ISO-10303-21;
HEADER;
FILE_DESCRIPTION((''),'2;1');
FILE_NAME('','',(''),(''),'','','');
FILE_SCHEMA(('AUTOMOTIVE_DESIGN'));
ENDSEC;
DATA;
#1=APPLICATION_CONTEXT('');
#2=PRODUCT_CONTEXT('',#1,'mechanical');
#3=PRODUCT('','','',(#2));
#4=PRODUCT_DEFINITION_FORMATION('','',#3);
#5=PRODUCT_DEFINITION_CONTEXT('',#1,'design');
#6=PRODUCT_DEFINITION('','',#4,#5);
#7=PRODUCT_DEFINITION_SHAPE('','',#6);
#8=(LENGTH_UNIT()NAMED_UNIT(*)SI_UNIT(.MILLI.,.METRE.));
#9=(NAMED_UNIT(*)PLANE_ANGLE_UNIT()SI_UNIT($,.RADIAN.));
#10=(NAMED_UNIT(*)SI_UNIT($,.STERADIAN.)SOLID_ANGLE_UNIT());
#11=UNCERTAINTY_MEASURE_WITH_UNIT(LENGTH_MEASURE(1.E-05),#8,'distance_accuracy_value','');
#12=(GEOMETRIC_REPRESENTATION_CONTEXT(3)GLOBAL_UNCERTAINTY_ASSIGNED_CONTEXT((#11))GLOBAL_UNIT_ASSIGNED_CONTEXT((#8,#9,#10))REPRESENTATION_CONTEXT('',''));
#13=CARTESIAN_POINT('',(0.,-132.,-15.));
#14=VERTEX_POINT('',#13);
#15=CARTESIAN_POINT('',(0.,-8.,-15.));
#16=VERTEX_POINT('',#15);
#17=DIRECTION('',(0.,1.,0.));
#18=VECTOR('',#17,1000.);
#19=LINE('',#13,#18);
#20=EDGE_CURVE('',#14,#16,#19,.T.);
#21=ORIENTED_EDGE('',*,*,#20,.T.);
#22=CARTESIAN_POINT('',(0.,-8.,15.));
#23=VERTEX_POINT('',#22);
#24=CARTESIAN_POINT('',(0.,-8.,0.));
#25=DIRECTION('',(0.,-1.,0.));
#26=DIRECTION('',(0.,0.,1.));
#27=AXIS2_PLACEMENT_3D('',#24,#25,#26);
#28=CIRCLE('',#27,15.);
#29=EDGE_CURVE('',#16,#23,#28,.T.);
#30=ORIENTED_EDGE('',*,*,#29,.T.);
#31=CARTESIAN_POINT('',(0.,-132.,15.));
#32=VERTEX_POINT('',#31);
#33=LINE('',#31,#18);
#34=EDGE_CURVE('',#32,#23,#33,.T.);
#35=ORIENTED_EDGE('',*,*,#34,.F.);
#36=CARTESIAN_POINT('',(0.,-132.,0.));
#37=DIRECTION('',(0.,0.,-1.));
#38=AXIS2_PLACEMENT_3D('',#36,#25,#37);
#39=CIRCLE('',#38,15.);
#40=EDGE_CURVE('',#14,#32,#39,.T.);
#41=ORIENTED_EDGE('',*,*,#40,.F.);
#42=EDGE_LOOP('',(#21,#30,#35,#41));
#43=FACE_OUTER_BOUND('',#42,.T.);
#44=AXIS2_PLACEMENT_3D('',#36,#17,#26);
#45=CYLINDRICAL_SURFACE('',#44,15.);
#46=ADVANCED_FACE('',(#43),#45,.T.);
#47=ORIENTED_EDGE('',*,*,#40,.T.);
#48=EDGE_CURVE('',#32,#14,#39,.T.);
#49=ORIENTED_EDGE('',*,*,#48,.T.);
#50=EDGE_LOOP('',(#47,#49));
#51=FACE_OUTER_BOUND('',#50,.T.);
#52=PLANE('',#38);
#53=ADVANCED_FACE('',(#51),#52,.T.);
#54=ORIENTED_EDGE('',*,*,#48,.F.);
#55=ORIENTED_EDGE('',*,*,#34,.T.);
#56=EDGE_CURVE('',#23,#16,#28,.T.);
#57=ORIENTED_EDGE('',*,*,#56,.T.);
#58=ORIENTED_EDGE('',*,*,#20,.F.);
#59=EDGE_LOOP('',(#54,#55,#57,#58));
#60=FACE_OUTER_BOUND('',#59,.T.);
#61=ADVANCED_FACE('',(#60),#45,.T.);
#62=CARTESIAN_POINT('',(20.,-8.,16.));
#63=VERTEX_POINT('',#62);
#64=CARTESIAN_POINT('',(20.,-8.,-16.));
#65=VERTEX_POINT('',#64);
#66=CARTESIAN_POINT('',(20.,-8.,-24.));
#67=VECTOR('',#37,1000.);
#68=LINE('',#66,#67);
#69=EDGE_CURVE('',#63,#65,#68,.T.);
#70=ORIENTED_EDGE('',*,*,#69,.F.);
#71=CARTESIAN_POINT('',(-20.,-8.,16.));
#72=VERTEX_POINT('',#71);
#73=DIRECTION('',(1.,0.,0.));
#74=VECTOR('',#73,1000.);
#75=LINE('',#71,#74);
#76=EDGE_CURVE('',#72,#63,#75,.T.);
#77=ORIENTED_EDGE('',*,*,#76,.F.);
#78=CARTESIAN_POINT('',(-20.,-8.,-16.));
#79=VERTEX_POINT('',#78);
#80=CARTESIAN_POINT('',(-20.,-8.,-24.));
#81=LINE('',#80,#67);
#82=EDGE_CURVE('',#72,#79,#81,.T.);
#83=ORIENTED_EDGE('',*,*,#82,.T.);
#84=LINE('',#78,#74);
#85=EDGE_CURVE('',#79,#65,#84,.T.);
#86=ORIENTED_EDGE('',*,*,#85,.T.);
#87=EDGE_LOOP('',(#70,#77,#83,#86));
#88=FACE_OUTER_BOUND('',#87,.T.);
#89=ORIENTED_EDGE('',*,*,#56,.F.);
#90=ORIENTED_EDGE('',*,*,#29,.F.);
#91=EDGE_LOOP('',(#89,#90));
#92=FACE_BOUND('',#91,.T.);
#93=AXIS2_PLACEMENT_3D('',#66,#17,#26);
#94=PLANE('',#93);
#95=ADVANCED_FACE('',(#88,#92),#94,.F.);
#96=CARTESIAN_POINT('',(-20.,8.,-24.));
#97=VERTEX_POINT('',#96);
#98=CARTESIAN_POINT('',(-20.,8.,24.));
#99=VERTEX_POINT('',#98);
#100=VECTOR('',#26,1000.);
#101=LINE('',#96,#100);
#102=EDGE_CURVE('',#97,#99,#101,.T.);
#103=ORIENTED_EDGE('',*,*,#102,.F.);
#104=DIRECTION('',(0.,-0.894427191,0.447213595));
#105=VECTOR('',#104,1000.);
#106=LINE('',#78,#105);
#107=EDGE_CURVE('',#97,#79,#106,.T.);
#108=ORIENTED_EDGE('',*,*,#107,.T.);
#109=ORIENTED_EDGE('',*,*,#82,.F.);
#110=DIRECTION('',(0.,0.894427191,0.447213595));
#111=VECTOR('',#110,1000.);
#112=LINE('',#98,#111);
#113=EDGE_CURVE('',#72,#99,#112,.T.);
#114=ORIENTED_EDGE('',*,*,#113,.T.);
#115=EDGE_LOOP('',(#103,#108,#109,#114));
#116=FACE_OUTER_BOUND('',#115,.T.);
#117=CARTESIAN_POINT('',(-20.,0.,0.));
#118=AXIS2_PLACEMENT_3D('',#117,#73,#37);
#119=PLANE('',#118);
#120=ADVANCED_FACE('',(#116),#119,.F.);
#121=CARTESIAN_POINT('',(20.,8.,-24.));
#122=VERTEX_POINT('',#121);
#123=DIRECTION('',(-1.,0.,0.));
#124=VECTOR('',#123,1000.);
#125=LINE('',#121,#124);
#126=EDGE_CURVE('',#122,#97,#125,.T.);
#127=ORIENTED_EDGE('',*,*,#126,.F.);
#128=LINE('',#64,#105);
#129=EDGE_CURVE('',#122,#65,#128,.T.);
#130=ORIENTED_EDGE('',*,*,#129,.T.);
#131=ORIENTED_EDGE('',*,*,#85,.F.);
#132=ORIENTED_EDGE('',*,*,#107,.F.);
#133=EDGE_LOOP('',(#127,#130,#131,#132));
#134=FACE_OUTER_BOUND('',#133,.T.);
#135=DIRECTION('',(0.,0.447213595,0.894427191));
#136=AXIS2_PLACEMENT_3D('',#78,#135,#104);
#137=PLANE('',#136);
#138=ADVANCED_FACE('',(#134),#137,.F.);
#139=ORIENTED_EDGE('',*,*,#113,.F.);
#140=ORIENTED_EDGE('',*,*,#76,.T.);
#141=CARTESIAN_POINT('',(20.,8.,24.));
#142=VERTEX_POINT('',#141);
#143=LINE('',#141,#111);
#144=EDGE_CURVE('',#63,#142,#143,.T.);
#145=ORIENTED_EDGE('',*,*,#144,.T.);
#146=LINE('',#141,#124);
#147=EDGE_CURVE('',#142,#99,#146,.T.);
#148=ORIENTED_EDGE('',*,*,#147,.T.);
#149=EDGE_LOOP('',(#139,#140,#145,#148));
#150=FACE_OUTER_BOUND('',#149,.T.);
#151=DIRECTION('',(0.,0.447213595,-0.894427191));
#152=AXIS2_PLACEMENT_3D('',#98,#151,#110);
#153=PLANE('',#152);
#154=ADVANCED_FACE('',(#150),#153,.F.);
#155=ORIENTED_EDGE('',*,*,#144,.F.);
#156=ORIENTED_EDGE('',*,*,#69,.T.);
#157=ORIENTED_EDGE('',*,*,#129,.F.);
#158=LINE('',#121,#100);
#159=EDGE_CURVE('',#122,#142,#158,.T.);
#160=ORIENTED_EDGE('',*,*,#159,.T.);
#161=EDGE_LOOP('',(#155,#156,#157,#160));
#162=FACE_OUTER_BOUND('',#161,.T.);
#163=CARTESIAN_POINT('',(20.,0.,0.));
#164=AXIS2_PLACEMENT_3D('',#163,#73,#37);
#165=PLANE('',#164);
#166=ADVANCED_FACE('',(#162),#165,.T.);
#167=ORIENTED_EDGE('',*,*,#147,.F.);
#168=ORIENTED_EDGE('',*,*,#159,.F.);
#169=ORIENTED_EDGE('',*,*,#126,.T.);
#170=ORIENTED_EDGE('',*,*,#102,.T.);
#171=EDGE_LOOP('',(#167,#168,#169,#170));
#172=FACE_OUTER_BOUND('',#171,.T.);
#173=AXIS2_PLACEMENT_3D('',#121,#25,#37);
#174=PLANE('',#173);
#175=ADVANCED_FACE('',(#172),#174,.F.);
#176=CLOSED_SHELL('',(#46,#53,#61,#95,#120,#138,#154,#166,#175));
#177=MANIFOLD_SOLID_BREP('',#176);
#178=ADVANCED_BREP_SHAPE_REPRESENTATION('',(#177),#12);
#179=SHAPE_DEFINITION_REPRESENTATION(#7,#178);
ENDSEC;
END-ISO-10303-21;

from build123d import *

# Parameters (mm, degrees)
SKETCH1_W               = 48
SKETCH1_H               = 16
BOSS_EXTRUDE1_DEPTH     = 20
CUT_EXTRUDE1_DEPTH      = 33.249030993
CUT_EXTRUDE1_DEPTH_BACK = 33.249030993
SKETCH3_R               = 15
BOSS_EXTRUDE2_DEPTH     = 124


with BuildPart() as part:
    # Sketch1 → Boss-Extrude1 (new, symmetric)
    with BuildSketch(Plane(origin=(0, 0, 0), x_dir=(0, 0, -1), z_dir=(1, 0, 0))):
        Rectangle(SKETCH1_W, SKETCH1_H)
    extrude(amount=BOSS_EXTRUDE1_DEPTH, both=True)

    # Sketch2 → Cut-Extrude1 (cut, two sides: drawn at the far end of the back side and taken through both)
    with BuildSketch(Plane(origin=(0, 0, 0), x_dir=(0, 0, -1), z_dir=(1, 0, 0)).offset(-CUT_EXTRUDE1_DEPTH_BACK)):
        Polygon((-24, 8), (-16, -8), (-24, -8), align=None)
        Polygon((24, 8), (24, -8), (16, -8), align=None)
    extrude(amount=CUT_EXTRUDE1_DEPTH + CUT_EXTRUDE1_DEPTH_BACK, mode=Mode.SUBTRACT)

    # Sketch3 → Boss-Extrude2 (add)
    with BuildSketch(Plane.XZ.offset(8)):
        with Locations(Location((0, 0, 0), (0, 0, 90))):
            Circle(SKETCH3_R)
    extrude(amount=BOSS_EXTRUDE2_DEPTH)


solid = part.part
